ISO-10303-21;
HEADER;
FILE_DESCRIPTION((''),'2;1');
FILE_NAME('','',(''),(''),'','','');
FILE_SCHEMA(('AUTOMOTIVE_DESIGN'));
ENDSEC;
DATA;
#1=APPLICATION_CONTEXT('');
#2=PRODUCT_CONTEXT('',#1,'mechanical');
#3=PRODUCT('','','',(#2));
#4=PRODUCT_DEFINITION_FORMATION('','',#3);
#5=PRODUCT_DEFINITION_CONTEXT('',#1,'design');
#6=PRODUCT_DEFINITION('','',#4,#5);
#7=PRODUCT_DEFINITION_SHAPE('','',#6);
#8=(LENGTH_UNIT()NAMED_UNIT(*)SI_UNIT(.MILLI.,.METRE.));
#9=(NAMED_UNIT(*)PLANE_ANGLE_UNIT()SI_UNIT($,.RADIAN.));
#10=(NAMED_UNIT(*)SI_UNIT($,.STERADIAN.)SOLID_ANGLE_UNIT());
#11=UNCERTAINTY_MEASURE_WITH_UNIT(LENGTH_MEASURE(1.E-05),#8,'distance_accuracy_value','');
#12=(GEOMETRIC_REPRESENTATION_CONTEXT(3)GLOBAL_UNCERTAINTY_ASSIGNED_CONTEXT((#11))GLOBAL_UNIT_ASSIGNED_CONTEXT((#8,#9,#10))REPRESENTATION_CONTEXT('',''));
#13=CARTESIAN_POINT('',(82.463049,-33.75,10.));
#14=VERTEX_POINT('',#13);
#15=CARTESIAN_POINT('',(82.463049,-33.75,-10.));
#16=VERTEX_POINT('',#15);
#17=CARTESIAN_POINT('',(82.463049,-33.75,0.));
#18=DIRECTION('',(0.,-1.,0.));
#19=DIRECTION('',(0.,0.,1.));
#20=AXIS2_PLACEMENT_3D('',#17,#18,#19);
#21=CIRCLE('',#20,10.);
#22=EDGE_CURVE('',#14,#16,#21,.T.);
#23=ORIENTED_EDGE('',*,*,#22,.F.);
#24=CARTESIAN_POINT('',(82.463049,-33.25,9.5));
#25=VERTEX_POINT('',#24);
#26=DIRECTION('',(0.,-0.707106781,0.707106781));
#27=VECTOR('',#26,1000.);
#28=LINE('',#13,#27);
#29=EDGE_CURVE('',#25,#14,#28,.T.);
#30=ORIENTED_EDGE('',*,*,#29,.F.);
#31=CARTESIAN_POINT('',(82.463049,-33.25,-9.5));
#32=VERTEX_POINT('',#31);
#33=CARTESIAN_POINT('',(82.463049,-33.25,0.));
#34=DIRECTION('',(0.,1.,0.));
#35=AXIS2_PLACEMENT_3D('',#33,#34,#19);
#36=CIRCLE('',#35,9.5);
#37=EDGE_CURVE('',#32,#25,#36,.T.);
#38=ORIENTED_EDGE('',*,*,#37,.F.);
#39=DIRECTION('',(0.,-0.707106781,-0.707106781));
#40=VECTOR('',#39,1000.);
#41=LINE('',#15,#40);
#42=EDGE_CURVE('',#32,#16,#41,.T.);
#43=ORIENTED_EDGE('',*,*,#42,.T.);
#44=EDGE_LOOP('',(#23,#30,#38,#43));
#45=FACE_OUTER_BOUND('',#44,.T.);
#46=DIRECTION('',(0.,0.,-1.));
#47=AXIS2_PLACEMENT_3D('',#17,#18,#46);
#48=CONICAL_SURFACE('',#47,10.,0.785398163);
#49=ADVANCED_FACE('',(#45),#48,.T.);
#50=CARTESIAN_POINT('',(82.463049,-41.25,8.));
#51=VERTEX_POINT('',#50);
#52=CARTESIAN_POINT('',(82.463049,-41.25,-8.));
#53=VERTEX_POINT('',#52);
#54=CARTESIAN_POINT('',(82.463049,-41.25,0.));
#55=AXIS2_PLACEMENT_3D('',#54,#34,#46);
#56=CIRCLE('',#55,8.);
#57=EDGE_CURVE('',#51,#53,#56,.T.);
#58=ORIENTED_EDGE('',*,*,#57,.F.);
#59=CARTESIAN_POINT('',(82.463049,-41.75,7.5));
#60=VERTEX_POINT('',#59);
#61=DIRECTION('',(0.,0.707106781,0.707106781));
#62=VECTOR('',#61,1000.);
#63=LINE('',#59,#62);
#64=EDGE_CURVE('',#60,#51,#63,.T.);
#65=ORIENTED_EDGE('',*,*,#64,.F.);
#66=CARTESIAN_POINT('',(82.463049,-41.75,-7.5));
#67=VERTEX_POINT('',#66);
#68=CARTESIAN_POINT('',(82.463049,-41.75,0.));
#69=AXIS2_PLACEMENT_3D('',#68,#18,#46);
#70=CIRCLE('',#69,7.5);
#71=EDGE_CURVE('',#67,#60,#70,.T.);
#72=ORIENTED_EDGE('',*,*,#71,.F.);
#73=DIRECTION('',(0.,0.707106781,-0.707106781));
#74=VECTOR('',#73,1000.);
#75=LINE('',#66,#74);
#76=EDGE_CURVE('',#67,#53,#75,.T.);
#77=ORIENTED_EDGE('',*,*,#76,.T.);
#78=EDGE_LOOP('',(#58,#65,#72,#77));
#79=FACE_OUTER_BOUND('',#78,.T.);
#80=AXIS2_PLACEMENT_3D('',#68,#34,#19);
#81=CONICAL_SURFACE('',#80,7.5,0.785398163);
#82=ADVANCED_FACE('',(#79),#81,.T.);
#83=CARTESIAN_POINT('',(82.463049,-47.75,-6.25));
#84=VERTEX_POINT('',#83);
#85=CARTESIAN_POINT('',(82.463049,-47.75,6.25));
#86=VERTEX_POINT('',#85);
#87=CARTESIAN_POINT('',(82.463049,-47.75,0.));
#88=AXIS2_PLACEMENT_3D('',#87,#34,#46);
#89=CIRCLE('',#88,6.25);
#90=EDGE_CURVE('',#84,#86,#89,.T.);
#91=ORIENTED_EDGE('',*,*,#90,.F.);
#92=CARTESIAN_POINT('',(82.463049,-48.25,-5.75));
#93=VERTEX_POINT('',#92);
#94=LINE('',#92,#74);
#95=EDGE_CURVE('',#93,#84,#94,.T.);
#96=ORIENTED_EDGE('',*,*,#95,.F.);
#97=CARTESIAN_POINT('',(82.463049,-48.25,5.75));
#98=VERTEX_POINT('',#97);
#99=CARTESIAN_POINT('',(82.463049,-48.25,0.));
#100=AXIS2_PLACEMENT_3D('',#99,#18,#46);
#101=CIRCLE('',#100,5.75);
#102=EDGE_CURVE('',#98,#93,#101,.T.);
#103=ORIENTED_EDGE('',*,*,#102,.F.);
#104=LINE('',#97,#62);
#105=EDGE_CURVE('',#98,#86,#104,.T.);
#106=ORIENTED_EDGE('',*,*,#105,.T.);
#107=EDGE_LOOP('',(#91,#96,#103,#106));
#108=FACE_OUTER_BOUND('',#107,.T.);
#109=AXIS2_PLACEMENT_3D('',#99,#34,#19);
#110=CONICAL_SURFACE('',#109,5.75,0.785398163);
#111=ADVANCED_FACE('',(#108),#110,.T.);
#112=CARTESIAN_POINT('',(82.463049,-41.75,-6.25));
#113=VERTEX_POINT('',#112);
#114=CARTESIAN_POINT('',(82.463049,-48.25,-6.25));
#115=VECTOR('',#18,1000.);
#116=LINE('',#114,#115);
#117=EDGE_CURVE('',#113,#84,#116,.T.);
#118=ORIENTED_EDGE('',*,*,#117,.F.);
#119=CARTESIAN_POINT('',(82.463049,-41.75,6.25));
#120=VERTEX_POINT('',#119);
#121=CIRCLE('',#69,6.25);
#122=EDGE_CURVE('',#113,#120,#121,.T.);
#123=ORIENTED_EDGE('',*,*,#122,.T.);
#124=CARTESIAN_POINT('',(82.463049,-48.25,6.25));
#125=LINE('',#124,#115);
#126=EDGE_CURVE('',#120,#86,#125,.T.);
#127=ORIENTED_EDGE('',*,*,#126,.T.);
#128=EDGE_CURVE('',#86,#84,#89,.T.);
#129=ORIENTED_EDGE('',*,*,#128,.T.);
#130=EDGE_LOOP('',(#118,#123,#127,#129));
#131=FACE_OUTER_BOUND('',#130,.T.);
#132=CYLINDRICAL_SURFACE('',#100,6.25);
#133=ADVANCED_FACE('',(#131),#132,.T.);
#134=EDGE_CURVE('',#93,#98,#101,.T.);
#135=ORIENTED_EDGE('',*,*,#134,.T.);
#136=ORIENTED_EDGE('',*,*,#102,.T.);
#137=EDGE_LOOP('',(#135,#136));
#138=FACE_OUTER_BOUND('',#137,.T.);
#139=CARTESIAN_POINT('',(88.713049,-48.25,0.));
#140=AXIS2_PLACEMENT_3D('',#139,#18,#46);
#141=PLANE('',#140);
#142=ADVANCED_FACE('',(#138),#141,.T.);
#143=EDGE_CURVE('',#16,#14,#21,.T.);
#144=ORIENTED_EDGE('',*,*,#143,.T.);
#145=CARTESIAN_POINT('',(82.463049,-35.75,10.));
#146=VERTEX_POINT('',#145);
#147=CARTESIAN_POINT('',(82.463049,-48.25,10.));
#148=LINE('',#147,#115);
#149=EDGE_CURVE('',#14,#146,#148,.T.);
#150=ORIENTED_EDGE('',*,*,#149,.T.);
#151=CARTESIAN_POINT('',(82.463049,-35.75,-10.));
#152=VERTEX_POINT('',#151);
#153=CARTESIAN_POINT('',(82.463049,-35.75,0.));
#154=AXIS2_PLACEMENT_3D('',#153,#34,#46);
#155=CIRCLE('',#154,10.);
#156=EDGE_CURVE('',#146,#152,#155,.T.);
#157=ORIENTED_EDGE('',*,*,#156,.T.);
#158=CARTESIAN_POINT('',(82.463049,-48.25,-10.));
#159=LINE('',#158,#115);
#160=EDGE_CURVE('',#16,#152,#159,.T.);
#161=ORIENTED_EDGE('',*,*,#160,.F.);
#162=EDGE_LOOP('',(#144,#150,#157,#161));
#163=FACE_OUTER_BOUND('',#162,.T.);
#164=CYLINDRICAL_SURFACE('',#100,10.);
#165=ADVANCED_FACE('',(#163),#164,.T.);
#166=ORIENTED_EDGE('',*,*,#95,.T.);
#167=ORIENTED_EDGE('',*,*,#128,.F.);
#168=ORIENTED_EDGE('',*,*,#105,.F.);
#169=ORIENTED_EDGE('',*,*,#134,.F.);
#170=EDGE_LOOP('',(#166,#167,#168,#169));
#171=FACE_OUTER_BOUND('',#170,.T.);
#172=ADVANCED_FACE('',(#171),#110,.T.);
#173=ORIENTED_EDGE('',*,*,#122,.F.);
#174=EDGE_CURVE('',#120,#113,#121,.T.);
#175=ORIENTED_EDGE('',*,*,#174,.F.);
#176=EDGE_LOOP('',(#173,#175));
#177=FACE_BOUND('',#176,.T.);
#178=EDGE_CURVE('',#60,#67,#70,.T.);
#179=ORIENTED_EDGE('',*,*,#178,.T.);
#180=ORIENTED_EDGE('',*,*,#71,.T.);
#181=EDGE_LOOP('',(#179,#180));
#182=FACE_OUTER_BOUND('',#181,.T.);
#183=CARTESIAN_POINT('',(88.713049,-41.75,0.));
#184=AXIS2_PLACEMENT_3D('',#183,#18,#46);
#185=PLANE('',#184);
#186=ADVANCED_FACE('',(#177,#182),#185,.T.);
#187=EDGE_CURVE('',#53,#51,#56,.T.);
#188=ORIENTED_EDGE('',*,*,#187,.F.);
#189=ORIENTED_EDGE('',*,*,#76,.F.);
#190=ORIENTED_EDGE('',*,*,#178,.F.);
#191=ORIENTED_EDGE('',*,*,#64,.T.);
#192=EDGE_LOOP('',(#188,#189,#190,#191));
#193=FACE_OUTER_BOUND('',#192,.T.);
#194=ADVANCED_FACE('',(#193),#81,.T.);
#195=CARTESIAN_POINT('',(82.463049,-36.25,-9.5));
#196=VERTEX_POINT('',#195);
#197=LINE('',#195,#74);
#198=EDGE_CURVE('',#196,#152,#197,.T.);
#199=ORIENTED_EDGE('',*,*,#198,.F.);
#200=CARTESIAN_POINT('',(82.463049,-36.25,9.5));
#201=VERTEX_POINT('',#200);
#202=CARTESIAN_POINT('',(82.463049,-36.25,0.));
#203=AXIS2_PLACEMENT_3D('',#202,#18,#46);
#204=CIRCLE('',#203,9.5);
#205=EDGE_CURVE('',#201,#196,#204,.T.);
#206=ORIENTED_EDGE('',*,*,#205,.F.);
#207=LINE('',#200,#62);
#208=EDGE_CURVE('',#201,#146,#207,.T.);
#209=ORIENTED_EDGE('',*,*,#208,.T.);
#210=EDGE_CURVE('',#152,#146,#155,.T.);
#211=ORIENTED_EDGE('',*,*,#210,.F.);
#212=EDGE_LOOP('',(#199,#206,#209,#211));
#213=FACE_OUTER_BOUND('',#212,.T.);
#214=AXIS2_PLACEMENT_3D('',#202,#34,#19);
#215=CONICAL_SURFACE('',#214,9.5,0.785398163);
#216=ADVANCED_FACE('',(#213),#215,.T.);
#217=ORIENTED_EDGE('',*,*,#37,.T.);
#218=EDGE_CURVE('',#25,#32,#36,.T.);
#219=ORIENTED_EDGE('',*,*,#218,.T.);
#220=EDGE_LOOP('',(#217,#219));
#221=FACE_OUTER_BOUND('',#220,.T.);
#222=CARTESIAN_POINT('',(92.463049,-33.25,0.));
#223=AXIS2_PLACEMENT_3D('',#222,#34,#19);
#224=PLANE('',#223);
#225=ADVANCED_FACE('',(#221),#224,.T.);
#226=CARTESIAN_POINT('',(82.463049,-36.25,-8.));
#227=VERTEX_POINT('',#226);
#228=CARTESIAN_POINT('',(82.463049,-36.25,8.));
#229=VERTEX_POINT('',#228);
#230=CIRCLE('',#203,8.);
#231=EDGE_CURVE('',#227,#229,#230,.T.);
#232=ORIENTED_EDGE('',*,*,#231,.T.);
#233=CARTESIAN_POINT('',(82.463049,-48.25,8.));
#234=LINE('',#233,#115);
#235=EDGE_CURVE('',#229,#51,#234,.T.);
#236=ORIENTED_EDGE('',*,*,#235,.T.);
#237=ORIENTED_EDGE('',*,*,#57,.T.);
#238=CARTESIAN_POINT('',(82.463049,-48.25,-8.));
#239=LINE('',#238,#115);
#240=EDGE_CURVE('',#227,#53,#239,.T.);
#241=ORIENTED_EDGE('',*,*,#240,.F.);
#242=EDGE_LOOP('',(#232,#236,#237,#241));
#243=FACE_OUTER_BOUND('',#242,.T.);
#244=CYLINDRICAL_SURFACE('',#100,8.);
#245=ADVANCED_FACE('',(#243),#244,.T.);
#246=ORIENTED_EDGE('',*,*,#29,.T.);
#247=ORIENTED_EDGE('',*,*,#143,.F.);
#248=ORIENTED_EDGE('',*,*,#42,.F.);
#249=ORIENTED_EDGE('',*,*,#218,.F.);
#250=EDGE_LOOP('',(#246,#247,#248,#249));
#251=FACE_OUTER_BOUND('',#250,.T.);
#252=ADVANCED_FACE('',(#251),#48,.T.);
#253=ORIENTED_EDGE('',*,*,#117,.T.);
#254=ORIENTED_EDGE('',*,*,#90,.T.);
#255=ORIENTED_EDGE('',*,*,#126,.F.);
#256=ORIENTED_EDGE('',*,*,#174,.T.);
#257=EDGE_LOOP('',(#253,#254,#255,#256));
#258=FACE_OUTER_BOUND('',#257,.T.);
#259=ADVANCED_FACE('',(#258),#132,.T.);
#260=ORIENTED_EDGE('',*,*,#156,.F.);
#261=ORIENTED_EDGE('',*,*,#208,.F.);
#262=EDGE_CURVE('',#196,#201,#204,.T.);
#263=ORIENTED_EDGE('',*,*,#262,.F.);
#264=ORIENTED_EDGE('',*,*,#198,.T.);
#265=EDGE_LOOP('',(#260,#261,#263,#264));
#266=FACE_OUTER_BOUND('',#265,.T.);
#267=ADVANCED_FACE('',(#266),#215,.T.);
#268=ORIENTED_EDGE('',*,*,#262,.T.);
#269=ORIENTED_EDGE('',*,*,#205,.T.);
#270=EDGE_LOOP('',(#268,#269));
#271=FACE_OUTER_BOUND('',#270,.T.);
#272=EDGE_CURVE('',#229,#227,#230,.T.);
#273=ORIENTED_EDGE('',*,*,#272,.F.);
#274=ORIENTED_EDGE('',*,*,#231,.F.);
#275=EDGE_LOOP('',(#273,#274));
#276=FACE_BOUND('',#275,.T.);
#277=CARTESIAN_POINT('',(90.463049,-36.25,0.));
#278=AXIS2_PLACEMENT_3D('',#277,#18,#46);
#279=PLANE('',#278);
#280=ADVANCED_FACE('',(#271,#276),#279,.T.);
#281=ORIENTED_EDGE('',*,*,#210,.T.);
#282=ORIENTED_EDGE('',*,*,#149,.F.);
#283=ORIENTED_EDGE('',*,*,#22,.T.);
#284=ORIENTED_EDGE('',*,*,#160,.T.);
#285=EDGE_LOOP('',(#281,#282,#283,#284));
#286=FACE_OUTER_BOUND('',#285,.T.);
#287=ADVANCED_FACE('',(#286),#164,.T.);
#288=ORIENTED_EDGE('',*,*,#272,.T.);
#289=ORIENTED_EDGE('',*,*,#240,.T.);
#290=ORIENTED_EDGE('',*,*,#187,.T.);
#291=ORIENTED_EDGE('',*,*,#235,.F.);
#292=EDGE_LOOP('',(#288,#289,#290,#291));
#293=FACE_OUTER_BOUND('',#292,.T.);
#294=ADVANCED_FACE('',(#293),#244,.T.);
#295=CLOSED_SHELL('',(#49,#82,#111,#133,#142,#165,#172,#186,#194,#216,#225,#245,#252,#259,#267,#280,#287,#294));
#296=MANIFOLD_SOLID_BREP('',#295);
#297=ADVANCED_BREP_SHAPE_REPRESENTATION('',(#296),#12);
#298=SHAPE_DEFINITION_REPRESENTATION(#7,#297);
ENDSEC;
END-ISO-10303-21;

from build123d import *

# Parameters (mm, degrees)
CHAMFER1_SIZE = 0.5


with BuildPart() as part:
    # Sketch1 → Revolve1 (revolve)
    with BuildSketch(Plane.XY, mode=Mode.PRIVATE) as revolve1_sk:
        Polygon((88.713048819, -48.25), (88.713048819, -41.75), (90.463048819, -41.75), (90.463048819, -36.25), (92.463048819, -36.25), (92.463048819, -33.25), (82.463048819, -33.25), (82.463048819, -48.25), align=None)
    revolve(revolve1_sk.sketch.rotate(Axis((82.463048819, -48.25, 0), (0, 1, 0)), 90), axis=Axis((82.463048819, -48.25, 0), (0, 1, 0)))

    # Chamfer1
    chamfer1_edges = [part.edges().sort_by_distance(p)[0] for p in [
        (82.463048819, -33.25, 10),
        (82.463048819, -36.25, 10),
        (82.463048819, -41.75, 8),
        (82.463048819, -48.25, 6.25),
    ]]
    chamfer(chamfer1_edges, length=CHAMFER1_SIZE)


solid = part.part
